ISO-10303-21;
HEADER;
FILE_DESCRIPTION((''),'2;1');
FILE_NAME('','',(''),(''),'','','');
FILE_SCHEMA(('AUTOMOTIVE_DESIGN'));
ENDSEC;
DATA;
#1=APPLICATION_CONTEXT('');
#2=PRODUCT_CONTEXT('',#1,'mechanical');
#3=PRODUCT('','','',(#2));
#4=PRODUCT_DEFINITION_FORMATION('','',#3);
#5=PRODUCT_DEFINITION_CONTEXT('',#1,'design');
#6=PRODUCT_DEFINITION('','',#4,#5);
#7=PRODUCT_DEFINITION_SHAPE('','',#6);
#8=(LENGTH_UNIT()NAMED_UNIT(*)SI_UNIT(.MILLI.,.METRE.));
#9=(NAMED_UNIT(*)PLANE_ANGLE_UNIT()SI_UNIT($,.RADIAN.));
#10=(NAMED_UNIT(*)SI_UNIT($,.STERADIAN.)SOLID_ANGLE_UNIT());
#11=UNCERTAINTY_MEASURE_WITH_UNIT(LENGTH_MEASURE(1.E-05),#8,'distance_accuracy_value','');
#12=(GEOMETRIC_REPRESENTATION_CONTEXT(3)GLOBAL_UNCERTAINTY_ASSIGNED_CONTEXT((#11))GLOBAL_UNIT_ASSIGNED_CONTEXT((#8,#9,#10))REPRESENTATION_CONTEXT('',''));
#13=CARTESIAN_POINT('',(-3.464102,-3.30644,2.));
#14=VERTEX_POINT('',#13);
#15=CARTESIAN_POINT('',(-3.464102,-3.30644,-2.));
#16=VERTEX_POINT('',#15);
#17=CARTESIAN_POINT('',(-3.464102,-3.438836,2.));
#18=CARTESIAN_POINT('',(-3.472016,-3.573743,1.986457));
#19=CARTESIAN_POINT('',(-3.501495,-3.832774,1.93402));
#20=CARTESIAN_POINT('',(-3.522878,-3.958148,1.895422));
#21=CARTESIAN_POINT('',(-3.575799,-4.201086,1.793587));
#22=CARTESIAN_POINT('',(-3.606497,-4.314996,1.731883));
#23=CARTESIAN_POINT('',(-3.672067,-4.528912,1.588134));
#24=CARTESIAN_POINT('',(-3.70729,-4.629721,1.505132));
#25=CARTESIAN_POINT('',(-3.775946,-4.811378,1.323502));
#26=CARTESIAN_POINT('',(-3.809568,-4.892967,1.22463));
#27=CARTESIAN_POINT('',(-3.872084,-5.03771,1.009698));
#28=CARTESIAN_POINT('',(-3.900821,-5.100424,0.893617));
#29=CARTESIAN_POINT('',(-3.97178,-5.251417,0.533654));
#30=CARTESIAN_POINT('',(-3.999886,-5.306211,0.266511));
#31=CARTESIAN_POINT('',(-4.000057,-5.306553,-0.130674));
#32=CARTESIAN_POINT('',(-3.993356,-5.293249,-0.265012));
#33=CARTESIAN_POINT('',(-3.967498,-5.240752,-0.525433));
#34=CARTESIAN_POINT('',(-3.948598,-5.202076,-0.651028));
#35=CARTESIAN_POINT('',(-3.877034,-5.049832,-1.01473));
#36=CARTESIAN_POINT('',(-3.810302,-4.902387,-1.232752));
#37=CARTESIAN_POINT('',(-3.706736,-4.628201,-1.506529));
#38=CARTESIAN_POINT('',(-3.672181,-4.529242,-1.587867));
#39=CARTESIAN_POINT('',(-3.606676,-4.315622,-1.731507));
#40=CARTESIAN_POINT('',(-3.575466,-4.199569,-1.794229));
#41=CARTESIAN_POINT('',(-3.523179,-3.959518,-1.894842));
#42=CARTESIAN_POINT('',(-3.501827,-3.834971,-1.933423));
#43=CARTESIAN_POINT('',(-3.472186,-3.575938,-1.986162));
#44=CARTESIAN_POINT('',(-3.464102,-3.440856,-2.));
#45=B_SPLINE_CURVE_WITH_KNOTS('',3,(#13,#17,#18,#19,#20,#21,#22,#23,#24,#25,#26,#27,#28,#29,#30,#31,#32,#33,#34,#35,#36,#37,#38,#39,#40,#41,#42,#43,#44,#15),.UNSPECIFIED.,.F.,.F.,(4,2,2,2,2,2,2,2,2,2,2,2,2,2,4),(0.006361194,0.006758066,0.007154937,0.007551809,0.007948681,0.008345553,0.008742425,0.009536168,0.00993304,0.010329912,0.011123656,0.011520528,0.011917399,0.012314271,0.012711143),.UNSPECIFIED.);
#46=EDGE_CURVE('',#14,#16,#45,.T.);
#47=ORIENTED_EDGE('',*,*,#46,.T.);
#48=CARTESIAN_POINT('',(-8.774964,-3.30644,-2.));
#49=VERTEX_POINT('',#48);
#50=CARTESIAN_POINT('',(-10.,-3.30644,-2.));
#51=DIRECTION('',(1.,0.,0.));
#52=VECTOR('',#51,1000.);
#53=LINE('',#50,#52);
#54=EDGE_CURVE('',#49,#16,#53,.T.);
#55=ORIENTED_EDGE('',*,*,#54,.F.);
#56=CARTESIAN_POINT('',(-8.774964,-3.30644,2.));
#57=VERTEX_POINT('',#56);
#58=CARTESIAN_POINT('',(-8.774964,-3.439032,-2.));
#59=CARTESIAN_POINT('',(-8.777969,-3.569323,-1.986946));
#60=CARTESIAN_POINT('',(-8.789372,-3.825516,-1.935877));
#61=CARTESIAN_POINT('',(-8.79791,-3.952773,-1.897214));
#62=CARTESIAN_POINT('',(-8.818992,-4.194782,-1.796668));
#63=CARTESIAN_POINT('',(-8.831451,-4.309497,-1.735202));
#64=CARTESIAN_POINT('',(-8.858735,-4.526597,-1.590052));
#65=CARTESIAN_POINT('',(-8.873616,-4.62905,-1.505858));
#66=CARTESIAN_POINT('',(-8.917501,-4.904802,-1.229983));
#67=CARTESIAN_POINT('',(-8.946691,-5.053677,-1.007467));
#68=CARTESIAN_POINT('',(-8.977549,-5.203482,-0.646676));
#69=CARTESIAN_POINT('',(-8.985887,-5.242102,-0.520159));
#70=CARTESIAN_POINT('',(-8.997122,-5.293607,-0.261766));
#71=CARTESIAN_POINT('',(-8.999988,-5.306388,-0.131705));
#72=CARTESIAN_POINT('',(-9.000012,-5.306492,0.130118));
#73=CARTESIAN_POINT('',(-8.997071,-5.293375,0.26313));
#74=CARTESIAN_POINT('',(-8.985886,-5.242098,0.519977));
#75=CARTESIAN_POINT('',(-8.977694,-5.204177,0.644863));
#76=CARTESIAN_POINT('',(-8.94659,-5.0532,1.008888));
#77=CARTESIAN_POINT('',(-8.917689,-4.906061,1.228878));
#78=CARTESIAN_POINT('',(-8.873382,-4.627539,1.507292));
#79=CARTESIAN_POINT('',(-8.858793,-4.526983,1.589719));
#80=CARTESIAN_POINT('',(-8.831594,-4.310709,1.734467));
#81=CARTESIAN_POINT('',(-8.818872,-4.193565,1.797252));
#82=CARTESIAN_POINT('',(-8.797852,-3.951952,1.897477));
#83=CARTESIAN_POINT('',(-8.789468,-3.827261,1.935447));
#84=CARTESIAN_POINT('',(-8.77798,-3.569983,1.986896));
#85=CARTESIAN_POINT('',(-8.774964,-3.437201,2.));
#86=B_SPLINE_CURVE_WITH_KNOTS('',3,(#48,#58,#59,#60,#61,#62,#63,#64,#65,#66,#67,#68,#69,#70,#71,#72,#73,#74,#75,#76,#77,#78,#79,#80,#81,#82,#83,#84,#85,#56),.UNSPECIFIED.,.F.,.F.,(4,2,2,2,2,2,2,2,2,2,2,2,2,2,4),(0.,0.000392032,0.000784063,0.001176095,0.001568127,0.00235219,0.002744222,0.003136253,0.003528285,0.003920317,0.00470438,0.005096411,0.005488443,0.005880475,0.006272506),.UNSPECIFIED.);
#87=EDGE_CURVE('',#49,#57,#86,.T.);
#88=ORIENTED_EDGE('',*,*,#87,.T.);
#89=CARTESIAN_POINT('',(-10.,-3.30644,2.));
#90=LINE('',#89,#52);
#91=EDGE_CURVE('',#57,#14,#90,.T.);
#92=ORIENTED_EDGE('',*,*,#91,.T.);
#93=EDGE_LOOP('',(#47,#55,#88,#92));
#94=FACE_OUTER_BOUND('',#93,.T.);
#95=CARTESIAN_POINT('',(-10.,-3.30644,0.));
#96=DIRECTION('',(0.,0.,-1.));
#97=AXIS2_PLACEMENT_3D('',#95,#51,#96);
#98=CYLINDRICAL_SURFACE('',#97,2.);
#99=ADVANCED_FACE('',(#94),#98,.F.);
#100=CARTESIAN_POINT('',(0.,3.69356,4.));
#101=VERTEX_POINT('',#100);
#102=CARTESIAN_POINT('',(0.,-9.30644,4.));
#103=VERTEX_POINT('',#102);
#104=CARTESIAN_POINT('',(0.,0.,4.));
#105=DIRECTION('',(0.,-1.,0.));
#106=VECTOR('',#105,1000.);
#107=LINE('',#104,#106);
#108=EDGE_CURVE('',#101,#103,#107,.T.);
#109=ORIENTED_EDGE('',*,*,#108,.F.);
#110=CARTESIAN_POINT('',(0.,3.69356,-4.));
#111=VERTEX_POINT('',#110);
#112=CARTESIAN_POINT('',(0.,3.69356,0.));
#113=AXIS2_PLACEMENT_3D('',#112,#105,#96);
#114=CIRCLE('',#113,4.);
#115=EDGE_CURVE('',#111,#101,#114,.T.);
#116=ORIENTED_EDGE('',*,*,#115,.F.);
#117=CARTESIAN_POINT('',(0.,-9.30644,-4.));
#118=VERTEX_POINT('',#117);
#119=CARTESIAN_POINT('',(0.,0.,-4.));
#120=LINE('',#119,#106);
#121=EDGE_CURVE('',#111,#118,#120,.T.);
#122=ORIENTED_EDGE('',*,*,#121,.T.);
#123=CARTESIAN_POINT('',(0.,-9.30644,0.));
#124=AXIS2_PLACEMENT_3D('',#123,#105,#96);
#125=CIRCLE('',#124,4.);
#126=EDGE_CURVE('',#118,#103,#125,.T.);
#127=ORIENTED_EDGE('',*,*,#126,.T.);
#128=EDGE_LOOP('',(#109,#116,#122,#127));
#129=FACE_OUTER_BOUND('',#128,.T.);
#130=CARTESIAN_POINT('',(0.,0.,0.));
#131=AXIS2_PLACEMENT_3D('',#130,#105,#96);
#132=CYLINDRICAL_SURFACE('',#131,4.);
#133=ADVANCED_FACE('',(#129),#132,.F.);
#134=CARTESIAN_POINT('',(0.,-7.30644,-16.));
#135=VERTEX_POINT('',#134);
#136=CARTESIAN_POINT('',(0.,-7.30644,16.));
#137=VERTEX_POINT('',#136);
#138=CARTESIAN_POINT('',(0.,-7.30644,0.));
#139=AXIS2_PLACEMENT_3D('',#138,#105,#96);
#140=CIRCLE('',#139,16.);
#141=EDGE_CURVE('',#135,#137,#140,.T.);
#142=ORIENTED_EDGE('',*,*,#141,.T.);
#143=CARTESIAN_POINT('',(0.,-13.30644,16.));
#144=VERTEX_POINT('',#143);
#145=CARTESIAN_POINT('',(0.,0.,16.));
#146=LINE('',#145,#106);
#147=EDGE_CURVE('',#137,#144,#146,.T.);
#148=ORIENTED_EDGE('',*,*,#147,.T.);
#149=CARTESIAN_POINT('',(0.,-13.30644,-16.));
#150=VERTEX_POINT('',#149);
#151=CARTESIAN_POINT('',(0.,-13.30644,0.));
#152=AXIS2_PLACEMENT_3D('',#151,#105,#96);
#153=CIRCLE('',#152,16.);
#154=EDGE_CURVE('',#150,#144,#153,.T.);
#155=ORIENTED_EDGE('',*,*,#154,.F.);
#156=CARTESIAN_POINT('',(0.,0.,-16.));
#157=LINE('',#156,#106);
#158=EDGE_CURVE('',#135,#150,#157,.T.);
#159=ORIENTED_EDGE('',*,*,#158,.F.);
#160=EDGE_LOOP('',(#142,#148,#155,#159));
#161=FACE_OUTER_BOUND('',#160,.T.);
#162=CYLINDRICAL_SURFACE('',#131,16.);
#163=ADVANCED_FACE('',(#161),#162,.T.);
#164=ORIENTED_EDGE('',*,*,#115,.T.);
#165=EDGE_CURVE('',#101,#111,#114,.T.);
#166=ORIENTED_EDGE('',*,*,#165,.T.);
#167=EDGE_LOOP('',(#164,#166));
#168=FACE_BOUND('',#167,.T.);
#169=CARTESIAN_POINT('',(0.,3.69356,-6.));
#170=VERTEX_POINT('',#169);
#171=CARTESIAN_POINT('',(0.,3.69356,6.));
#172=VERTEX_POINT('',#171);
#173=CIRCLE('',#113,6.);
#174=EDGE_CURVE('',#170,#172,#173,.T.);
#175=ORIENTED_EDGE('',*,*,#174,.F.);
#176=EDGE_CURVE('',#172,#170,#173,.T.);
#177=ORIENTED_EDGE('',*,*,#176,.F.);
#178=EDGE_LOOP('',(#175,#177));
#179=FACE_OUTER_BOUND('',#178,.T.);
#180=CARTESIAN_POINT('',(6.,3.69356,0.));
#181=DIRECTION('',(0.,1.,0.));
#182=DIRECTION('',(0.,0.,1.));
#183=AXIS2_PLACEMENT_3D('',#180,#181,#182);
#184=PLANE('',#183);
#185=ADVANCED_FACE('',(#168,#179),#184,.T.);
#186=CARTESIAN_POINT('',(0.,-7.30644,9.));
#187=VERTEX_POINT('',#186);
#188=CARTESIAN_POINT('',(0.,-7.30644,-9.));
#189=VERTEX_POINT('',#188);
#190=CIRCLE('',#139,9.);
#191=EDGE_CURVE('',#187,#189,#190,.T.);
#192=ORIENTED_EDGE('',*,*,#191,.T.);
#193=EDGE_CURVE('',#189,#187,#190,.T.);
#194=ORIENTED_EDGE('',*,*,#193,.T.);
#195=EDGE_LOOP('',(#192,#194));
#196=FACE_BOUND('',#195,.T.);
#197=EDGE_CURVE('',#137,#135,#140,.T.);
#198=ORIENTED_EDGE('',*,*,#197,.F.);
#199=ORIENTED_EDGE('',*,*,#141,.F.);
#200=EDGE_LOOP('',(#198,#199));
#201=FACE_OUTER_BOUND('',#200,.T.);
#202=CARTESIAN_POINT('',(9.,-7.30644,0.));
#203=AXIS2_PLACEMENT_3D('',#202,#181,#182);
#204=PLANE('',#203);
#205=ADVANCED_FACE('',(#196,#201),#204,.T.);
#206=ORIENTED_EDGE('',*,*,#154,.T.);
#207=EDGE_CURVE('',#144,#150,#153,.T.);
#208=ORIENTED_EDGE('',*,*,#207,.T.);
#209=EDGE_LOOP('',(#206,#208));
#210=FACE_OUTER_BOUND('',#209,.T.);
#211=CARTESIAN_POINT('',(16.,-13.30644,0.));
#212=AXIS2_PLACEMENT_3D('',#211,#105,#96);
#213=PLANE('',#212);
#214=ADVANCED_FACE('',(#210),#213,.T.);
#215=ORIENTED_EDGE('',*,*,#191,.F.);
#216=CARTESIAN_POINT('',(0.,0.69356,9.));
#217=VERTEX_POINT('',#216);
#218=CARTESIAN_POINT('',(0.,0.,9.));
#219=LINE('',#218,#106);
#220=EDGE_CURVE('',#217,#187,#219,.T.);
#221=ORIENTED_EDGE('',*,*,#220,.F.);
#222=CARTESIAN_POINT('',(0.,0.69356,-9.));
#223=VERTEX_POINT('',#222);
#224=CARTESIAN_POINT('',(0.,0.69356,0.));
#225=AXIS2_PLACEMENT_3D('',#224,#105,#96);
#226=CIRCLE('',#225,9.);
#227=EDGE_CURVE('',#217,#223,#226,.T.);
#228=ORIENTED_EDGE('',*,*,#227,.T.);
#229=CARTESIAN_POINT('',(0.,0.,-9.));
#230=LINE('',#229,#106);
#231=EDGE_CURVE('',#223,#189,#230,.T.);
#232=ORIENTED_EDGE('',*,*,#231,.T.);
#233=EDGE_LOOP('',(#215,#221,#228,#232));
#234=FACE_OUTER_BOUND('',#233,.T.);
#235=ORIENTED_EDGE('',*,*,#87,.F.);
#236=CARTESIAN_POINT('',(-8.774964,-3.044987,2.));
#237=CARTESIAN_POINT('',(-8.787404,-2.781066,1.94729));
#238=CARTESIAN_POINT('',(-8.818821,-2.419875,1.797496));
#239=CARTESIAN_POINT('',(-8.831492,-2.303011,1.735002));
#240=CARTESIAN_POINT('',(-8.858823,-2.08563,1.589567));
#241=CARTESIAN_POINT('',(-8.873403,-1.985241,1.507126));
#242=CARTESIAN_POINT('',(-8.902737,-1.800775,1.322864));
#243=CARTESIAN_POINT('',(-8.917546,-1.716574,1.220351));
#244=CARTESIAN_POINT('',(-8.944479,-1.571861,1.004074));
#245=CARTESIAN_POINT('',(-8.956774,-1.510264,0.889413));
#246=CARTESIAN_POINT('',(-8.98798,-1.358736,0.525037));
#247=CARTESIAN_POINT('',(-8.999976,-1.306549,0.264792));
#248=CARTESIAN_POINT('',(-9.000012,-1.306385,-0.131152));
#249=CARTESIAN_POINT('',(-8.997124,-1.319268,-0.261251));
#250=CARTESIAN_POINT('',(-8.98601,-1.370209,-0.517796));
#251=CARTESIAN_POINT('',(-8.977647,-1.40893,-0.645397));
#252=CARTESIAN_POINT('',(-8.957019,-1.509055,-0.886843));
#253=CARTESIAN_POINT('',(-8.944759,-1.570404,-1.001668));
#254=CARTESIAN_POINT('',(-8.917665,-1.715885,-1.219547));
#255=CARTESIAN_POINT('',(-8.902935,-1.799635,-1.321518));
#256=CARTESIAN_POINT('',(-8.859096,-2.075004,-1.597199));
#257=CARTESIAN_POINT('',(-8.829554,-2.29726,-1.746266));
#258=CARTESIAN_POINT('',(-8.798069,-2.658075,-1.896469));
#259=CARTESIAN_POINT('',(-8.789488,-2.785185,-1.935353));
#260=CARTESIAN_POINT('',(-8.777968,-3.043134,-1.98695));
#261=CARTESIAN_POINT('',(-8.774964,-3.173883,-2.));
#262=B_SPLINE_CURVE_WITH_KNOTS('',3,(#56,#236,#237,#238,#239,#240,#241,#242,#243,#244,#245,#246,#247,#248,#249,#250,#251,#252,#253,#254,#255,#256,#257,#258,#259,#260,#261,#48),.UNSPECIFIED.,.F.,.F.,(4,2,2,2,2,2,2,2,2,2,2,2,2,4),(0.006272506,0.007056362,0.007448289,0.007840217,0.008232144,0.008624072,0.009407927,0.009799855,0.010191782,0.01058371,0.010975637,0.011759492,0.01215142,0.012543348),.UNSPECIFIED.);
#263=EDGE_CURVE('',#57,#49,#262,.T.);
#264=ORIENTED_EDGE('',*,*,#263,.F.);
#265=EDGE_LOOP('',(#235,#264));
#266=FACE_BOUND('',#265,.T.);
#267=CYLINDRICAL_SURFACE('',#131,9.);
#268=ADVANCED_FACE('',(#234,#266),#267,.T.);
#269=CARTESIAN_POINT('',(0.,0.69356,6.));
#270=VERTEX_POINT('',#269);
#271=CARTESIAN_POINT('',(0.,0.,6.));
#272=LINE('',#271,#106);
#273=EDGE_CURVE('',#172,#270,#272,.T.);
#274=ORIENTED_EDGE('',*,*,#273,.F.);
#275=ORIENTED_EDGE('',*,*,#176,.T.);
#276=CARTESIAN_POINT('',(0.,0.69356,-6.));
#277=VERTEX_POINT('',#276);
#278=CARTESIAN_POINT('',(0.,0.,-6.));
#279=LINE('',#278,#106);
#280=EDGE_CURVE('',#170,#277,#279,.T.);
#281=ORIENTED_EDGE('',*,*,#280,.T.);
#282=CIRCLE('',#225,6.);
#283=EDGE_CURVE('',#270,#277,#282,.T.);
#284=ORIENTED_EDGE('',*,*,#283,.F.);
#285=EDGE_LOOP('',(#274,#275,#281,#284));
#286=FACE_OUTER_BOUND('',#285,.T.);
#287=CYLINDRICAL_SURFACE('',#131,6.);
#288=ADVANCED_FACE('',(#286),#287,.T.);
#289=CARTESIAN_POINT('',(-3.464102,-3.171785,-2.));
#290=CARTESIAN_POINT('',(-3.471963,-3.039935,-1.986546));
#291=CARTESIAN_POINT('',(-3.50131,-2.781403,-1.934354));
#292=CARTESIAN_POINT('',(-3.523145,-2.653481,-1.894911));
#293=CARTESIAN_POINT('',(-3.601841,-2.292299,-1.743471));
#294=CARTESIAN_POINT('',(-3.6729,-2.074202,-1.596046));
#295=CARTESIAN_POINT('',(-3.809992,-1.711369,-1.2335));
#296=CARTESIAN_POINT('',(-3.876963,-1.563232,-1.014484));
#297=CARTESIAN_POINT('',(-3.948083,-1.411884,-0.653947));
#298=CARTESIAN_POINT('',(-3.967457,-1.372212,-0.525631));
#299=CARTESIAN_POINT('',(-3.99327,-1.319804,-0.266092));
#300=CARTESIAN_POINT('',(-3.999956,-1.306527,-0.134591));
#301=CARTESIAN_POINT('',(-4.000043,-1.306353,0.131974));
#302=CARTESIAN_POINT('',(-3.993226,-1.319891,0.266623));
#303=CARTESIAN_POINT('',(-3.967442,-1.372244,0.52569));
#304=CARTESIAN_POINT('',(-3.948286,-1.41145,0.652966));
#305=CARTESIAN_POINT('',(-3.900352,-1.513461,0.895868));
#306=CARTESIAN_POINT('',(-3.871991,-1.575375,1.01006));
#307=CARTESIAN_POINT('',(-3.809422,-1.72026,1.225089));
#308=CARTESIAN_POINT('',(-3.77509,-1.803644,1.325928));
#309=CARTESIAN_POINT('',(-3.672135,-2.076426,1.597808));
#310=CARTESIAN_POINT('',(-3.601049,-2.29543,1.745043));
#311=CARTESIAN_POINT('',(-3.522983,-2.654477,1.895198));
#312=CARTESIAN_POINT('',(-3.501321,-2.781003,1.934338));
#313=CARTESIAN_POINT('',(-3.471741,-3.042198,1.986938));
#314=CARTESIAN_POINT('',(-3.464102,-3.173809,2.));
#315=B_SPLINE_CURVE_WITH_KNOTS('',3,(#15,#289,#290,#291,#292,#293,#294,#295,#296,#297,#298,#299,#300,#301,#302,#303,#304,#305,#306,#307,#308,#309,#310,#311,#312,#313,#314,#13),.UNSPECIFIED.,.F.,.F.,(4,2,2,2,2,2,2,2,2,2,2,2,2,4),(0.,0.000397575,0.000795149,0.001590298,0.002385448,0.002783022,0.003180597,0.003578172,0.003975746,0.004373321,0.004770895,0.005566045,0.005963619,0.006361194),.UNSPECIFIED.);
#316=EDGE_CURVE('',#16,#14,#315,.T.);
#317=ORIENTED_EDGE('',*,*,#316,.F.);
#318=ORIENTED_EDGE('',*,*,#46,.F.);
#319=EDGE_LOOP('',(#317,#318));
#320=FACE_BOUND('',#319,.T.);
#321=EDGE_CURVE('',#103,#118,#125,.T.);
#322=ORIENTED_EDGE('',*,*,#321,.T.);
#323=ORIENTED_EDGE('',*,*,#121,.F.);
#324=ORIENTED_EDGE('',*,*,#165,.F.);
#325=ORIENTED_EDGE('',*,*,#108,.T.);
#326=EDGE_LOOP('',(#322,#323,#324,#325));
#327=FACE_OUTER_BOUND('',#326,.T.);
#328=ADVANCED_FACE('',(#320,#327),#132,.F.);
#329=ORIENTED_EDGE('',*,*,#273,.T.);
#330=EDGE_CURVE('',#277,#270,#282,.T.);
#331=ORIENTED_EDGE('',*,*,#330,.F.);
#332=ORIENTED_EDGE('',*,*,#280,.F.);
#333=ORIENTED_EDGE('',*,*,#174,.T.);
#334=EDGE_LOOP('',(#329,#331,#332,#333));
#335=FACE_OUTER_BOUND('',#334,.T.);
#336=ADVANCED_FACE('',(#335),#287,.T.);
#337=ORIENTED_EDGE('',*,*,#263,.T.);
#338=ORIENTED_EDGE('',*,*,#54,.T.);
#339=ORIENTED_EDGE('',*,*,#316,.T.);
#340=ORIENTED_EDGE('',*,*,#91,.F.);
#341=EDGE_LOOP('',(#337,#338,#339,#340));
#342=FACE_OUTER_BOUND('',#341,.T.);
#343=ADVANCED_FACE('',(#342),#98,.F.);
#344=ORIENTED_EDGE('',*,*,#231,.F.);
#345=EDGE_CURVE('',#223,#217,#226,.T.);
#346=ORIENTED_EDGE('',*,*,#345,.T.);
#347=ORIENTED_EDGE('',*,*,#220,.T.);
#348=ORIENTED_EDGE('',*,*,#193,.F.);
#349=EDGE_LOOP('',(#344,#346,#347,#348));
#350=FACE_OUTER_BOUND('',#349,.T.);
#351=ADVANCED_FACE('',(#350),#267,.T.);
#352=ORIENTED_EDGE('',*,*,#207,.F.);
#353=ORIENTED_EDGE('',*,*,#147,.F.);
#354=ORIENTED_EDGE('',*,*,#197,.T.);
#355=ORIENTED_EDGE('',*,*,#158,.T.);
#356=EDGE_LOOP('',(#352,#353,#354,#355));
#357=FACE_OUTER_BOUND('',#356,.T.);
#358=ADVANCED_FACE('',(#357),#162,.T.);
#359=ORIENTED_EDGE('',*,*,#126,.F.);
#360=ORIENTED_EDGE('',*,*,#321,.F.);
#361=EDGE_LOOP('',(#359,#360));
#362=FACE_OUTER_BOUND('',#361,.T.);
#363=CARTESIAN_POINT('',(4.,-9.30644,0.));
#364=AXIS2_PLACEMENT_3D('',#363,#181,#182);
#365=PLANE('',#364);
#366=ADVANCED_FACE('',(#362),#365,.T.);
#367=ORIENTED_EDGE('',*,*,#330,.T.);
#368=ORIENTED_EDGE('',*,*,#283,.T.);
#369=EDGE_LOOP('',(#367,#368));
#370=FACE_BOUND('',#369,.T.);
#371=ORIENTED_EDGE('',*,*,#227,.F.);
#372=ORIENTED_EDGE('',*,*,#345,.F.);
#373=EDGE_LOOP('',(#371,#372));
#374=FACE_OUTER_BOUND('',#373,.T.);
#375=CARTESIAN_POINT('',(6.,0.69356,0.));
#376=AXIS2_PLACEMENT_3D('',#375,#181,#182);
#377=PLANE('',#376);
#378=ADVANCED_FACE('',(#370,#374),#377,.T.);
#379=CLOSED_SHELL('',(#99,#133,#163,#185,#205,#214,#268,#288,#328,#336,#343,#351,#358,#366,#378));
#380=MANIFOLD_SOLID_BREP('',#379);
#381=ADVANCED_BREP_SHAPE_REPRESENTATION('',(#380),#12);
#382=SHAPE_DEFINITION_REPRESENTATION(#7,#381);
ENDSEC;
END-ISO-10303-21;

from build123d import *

# Parameters (mm, degrees)
SKETCH_2_R          = 2
CUT_EXTRUDE_1_DEPTH = 10


with BuildPart() as part:
    # 草图1 → 旋转1 (revolve)
    with BuildSketch(Plane.XY, mode=Mode.PRIVATE) as revolve_1_sk:
        Polygon((6, 3.693560261), (6, 0.693560261), (9, 0.693560261), (9, -7.306439739), (16, -7.306439739), (16, -13.306439739), (0, -13.306439739), (0, -9.306439739), (4, -9.306439739), (4, 3.693560261), align=None)
    revolve(revolve_1_sk.sketch.rotate(Axis((0, 0, 0), (0, 1, 0)), 90), axis=Axis((0, 0, 0), (0, 1, 0)))

    # 草图2 → 切除-拉伸1 (cut)
    with BuildSketch(Plane(origin=(0, 0, 0), x_dir=(0, 0, -1), z_dir=(1, 0, 0))):
        with Locations((0, -3.306439739)):
            Circle(SKETCH_2_R)
    extrude(amount=-CUT_EXTRUDE_1_DEPTH, mode=Mode.SUBTRACT)


solid = part.part
